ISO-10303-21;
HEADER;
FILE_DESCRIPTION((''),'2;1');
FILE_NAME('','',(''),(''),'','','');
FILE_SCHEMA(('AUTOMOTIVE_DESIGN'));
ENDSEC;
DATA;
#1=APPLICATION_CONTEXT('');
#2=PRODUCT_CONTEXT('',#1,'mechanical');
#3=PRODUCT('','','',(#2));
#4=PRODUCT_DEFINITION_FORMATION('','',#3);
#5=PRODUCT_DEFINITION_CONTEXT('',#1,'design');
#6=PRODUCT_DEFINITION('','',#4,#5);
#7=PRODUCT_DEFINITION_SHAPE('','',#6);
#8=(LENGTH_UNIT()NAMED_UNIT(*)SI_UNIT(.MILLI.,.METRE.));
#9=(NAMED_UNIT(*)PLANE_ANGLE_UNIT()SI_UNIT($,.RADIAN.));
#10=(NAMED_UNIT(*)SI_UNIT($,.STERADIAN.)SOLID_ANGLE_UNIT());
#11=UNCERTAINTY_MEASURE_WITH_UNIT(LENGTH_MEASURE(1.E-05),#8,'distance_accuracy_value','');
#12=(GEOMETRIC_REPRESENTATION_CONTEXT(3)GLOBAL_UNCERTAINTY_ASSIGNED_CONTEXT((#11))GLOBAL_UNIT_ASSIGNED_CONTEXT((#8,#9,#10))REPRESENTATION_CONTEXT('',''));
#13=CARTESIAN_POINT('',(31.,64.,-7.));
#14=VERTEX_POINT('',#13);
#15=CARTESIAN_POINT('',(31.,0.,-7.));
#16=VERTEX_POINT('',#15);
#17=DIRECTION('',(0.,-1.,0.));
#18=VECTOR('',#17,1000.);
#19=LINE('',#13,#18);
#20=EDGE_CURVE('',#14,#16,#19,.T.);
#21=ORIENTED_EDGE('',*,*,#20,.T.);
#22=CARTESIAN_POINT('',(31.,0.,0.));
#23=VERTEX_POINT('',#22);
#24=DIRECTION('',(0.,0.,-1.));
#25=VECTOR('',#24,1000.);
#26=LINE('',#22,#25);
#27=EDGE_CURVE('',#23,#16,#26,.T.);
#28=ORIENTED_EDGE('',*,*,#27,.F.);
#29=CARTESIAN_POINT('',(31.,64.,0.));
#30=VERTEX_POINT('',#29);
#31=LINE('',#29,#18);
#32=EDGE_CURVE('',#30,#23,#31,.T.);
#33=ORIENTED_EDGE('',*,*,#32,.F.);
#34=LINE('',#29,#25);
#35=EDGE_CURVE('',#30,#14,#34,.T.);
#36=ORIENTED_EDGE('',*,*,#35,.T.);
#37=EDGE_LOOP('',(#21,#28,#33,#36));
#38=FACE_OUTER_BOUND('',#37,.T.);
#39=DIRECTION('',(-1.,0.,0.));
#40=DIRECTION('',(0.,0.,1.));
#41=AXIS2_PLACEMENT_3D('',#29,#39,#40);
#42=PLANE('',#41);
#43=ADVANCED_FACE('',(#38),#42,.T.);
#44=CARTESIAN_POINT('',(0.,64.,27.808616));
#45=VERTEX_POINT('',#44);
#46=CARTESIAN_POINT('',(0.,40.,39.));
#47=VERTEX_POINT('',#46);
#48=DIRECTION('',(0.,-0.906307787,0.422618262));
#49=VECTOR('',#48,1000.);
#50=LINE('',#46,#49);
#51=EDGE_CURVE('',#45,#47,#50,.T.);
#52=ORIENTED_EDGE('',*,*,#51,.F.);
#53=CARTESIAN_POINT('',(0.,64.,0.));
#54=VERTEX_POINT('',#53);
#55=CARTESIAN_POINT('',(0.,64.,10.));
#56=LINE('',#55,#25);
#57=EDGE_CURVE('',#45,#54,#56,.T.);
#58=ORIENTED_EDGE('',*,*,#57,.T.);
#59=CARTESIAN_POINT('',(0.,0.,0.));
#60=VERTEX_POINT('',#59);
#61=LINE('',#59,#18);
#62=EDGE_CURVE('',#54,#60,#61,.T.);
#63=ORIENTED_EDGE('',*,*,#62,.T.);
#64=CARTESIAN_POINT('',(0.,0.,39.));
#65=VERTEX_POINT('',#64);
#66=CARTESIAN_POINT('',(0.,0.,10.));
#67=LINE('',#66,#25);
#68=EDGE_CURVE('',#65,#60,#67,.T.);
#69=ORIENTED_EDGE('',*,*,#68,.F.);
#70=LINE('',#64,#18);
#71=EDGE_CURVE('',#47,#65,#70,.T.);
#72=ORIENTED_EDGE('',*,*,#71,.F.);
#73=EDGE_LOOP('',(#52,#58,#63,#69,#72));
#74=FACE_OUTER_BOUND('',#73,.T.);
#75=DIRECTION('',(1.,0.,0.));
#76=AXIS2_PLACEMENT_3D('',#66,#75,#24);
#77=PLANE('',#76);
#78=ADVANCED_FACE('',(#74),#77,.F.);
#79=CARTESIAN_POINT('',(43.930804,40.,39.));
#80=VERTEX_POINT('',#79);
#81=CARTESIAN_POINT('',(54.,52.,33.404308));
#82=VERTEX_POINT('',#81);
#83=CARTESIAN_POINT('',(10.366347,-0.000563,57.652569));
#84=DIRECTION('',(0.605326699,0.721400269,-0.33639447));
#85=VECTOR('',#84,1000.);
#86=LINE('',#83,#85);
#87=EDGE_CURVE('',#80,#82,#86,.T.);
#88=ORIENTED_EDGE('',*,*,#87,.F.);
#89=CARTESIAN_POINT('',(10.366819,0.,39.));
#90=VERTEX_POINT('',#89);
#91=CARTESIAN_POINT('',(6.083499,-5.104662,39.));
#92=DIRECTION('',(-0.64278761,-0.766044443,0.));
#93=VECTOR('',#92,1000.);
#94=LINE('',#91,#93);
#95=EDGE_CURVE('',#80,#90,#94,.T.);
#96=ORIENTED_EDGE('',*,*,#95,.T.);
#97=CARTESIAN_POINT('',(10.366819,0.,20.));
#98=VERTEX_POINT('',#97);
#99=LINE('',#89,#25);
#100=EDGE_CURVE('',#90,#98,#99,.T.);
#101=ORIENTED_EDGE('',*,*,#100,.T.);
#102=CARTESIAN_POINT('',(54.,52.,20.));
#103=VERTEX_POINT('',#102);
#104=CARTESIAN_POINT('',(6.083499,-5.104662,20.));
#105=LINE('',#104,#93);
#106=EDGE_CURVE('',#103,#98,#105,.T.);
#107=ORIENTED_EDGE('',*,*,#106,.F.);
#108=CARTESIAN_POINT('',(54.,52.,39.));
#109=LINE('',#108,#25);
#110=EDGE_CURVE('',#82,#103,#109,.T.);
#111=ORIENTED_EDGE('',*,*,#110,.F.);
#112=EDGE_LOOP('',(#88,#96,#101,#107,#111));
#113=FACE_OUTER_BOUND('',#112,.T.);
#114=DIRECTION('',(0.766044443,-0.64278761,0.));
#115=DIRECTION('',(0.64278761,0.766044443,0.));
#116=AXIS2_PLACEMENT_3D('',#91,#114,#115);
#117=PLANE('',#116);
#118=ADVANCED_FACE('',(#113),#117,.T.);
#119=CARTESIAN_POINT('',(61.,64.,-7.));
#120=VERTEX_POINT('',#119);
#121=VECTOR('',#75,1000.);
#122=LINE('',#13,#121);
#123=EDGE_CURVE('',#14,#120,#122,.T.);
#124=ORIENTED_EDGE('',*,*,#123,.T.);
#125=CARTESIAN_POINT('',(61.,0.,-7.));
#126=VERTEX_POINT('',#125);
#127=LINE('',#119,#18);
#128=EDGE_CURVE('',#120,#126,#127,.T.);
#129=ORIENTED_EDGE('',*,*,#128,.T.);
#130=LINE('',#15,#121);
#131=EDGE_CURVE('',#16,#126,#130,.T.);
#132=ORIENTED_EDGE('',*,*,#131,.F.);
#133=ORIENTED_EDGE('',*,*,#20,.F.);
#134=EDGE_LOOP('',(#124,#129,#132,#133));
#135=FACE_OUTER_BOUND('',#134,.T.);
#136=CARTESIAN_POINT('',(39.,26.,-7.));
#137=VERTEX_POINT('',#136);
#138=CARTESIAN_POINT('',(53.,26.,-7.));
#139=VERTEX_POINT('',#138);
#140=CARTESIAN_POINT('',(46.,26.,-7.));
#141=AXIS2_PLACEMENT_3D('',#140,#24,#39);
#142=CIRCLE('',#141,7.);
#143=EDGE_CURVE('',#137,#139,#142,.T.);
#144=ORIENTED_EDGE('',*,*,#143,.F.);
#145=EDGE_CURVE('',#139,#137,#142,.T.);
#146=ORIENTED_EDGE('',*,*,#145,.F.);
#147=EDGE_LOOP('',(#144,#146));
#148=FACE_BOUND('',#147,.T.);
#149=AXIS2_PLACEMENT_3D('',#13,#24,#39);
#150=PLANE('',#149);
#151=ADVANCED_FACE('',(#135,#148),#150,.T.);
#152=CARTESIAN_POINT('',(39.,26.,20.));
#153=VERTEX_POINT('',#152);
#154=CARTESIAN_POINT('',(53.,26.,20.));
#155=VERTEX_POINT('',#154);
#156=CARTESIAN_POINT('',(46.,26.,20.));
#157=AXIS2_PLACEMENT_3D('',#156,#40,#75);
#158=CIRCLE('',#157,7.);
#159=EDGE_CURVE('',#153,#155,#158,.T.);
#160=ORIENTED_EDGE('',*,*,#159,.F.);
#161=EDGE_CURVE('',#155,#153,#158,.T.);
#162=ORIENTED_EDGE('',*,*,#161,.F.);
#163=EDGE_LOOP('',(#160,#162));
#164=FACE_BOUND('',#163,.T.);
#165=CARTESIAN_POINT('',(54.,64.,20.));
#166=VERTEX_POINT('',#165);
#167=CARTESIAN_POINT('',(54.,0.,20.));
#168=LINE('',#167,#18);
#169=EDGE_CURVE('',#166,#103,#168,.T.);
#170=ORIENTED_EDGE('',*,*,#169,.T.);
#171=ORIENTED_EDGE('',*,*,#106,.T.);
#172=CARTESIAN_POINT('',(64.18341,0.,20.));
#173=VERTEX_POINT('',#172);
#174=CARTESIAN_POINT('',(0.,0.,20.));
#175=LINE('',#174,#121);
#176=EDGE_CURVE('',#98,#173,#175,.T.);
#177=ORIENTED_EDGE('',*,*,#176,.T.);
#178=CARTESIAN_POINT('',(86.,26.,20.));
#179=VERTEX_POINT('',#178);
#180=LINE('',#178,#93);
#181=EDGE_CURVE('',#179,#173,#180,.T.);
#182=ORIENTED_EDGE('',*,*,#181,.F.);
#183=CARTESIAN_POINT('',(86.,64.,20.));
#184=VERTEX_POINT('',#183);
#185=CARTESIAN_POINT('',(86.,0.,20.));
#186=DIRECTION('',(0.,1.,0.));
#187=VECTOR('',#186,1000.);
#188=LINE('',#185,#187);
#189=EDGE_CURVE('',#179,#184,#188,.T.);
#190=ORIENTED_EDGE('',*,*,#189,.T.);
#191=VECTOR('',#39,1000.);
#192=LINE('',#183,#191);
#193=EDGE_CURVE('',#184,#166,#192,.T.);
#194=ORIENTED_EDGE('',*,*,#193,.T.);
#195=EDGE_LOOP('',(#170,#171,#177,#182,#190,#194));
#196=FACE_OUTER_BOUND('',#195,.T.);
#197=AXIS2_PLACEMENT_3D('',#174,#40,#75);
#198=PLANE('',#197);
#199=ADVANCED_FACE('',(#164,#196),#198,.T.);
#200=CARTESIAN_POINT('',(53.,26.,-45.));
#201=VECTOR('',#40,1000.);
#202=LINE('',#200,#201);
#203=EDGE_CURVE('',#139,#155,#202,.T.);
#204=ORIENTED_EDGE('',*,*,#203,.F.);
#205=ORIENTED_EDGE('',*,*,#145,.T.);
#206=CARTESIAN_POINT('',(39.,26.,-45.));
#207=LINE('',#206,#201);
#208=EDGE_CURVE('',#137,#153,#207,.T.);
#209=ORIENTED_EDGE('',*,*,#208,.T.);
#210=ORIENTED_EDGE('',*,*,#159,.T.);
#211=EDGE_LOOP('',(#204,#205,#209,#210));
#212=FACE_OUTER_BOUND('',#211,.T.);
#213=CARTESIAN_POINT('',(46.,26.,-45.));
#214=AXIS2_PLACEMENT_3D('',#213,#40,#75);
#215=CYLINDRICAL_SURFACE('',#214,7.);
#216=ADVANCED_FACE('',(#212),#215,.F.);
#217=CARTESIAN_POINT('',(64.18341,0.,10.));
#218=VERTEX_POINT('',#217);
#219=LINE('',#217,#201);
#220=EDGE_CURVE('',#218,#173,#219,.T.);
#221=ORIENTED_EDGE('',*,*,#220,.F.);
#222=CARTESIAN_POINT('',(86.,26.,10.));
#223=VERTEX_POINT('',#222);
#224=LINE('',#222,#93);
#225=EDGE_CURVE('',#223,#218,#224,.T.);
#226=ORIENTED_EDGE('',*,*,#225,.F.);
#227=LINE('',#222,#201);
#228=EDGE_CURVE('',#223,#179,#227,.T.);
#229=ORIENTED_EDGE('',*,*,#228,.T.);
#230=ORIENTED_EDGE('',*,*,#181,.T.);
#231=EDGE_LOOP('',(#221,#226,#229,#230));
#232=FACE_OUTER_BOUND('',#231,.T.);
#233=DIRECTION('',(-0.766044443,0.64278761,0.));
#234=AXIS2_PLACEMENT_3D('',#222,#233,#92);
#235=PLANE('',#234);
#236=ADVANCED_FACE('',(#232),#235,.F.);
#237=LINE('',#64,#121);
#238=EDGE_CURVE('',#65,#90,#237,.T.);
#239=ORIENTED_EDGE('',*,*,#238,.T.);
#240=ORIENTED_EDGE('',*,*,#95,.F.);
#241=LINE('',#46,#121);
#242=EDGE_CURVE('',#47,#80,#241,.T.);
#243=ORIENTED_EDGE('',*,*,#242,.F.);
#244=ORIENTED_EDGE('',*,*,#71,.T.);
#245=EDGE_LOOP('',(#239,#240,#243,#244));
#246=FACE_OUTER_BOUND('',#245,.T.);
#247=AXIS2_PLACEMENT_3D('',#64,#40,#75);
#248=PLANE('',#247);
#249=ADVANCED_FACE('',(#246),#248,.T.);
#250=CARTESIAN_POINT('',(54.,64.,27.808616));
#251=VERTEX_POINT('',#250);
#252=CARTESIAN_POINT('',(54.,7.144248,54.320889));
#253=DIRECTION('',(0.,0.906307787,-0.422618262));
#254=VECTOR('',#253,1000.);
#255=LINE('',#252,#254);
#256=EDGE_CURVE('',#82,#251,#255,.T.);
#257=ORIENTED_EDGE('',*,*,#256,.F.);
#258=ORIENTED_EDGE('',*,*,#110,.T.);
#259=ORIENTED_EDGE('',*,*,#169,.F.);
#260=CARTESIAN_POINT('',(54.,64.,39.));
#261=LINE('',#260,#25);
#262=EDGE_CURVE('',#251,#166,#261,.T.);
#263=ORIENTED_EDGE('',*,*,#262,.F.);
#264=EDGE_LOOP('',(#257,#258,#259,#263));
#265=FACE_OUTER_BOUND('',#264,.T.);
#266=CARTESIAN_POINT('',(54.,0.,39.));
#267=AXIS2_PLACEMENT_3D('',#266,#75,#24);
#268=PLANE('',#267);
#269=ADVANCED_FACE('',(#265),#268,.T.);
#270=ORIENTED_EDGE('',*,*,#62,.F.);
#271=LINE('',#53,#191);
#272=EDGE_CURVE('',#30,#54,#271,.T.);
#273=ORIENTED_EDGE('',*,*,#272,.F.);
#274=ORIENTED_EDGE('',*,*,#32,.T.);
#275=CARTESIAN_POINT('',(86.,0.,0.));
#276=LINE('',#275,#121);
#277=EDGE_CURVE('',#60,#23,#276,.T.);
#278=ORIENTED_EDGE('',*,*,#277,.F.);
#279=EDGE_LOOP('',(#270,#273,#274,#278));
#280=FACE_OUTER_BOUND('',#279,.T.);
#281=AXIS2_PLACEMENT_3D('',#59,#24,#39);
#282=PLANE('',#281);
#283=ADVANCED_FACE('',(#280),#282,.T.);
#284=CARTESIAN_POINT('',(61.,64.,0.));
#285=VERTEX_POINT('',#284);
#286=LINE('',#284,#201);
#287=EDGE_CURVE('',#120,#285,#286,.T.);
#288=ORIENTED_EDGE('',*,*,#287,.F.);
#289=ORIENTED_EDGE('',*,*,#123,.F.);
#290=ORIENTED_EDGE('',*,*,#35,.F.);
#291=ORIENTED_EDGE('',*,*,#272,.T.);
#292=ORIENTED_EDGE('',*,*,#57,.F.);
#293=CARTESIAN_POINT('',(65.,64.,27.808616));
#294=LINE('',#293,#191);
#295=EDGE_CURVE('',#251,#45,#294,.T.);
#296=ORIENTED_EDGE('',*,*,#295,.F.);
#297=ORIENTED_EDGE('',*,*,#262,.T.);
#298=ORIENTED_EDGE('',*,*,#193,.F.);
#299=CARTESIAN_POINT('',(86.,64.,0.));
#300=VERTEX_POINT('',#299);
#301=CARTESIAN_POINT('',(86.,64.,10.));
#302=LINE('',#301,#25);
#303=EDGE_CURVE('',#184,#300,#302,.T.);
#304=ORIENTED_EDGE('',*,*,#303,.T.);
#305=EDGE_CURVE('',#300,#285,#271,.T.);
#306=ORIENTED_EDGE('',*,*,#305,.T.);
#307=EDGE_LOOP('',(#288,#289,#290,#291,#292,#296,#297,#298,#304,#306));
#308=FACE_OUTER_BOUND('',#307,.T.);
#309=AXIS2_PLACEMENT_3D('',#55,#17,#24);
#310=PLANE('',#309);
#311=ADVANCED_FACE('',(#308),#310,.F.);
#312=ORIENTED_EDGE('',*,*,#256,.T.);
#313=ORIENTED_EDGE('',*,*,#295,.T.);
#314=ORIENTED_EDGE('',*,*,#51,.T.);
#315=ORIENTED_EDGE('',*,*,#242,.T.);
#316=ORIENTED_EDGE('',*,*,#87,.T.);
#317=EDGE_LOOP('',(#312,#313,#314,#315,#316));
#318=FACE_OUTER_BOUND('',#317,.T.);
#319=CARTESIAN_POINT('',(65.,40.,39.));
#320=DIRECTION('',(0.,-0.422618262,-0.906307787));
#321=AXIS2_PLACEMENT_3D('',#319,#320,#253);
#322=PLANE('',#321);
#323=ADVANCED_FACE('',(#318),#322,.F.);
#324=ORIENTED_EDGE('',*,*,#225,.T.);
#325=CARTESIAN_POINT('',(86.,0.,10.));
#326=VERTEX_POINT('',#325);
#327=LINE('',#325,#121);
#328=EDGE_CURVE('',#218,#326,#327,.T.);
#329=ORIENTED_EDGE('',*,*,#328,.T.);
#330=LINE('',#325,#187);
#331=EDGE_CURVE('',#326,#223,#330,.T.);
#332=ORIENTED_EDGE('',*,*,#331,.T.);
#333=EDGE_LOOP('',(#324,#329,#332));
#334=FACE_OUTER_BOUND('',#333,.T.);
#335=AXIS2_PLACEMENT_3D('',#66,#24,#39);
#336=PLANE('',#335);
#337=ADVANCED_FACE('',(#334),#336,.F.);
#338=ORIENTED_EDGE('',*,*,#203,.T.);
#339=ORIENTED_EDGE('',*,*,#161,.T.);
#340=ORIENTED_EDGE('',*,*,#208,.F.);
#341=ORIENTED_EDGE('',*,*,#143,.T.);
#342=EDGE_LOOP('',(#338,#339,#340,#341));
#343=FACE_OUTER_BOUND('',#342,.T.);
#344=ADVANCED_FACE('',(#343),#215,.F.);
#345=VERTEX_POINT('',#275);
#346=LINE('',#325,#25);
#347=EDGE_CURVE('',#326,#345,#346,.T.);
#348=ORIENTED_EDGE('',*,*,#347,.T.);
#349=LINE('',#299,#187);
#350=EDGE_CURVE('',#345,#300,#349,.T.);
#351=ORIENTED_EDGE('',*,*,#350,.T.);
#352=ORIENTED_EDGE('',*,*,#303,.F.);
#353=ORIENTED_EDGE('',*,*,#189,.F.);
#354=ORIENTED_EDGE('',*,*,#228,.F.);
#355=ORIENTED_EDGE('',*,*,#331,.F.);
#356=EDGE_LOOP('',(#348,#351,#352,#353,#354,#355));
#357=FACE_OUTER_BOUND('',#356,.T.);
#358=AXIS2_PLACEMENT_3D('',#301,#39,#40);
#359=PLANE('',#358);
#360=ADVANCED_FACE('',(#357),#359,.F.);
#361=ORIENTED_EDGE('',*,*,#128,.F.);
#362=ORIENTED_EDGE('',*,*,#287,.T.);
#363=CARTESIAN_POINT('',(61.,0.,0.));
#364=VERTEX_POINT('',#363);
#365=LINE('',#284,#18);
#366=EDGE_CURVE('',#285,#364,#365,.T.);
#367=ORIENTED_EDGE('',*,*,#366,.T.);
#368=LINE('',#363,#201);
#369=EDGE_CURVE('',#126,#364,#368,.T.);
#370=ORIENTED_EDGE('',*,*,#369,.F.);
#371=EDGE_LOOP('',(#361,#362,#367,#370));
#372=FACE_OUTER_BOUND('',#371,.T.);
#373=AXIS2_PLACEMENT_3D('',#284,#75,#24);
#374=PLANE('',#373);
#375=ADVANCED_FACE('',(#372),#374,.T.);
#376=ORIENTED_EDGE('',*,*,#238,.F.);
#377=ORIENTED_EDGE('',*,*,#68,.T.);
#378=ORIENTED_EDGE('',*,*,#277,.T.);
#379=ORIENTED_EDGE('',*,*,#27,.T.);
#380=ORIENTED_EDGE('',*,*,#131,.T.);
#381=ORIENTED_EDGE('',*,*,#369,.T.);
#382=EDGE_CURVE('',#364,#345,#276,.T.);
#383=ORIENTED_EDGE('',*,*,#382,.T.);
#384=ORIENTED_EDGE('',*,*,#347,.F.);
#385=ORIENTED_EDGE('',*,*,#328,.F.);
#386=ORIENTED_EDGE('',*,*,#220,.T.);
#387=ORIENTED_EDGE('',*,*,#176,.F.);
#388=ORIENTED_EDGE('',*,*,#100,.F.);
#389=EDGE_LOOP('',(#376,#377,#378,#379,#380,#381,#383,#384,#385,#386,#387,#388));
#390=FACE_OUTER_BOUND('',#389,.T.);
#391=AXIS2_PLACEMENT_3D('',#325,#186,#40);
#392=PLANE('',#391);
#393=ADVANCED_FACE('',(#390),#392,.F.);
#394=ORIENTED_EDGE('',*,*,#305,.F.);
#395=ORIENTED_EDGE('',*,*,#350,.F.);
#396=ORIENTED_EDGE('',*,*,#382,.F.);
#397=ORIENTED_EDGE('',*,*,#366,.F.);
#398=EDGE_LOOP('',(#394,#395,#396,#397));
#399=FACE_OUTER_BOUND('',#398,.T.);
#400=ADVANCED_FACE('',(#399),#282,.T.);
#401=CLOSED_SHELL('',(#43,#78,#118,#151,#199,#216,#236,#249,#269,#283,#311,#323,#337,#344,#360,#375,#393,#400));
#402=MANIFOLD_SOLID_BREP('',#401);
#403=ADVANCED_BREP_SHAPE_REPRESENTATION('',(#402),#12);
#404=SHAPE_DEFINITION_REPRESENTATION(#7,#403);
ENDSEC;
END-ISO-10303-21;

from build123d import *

# Parameters (mm, degrees)
BASE_PLATE_SKETCH_W        = 86
BASE_PLATE_SKETCH_H        = 64
BASE_PLATE_86X64X10_DEPTH  = 10
UPPER_LAYER_SKETCH_W       = 86
UPPER_LAYER_SKETCH_H       = 64
UPPER_LAYER_BOSS_10_DEPTH  = 10
ANGLED_STEP_BOSS_19_DEPTH  = 19
ANGLED_CUT_25DEG_DEPTH     = 65
THROUGH_HOLE_SKETCH_R      = 7
THROUGH_HOLE_14_DEPTH      = 65
TRIANGULAR_NOTCH_CUT_DEPTH = 10
SIDE_BOSS_SKETCH_W         = 30
SIDE_BOSS_SKETCH_H         = 7
SIDE_BOSS_64_DEPTH         = 64
SIDE_BOSS_HOLE_SKETCH_R    = 7
SIDE_BOSS_HOLE_14_DEPTH    = 64


with BuildPart() as part:
    # Base Plate Sketch → Base Plate 86x64x10 (new body)
    with BuildSketch(Plane.XY):
        with Locations((43, 32)):
            Rectangle(BASE_PLATE_SKETCH_W, BASE_PLATE_SKETCH_H)
    extrude(amount=BASE_PLATE_86X64X10_DEPTH)

    # Upper Layer Sketch → Upper Layer Boss 10 (add)
    with BuildSketch(Plane.XY.offset(10)):
        with Locations((43, 32)):
            Rectangle(UPPER_LAYER_SKETCH_W, UPPER_LAYER_SKETCH_H)
    extrude(amount=UPPER_LAYER_BOSS_10_DEPTH)

    # Angled Step Sketch → Angled Step Boss 19 (add)
    with BuildSketch(Plane.XY.offset(20)):
        Polygon((54, 52), (54, 64), (0, 64), (0, 0), (10.366819179, 0), align=None)
    extrude(amount=ANGLED_STEP_BOSS_19_DEPTH)

    # Angled Cut Sketch → Angled Cut 25deg (cut)
    with BuildSketch(Plane.ZY):
        Polygon((39, 64), (39, 40), (27.808616204, 64), align=None)
    extrude(amount=-ANGLED_CUT_25DEG_DEPTH, mode=Mode.SUBTRACT)

    # Through Hole Sketch → Through Hole Ø14 (cut)
    with BuildSketch(Plane.XY.offset(20)):
        with Locations((46, 26)):
            Circle(THROUGH_HOLE_SKETCH_R)
    extrude(amount=-THROUGH_HOLE_14_DEPTH, mode=Mode.SUBTRACT)

    # Triangular Notch Sketch → Triangular Notch Cut (cut)
    with BuildSketch(Plane.XY.offset(20)):
        Polygon((86, 0), (86, 26), (64.183409589, 0), align=None)
    extrude(amount=-TRIANGULAR_NOTCH_CUT_DEPTH, mode=Mode.SUBTRACT)

    # Side Boss Sketch → Side Boss 64 (add)
    with BuildSketch(Plane.XZ):
        with Locations((46, -3.5)):
            Rectangle(SIDE_BOSS_SKETCH_W, SIDE_BOSS_SKETCH_H)
    extrude(amount=-SIDE_BOSS_64_DEPTH)

    # Side Boss Hole Sketch → Side Boss Hole Ø14 (cut)
    with BuildSketch(Plane.XY):
        with Locations((46, 26)):
            Circle(SIDE_BOSS_HOLE_SKETCH_R)
    extrude(amount=-SIDE_BOSS_HOLE_14_DEPTH, mode=Mode.SUBTRACT)


solid = part.part
